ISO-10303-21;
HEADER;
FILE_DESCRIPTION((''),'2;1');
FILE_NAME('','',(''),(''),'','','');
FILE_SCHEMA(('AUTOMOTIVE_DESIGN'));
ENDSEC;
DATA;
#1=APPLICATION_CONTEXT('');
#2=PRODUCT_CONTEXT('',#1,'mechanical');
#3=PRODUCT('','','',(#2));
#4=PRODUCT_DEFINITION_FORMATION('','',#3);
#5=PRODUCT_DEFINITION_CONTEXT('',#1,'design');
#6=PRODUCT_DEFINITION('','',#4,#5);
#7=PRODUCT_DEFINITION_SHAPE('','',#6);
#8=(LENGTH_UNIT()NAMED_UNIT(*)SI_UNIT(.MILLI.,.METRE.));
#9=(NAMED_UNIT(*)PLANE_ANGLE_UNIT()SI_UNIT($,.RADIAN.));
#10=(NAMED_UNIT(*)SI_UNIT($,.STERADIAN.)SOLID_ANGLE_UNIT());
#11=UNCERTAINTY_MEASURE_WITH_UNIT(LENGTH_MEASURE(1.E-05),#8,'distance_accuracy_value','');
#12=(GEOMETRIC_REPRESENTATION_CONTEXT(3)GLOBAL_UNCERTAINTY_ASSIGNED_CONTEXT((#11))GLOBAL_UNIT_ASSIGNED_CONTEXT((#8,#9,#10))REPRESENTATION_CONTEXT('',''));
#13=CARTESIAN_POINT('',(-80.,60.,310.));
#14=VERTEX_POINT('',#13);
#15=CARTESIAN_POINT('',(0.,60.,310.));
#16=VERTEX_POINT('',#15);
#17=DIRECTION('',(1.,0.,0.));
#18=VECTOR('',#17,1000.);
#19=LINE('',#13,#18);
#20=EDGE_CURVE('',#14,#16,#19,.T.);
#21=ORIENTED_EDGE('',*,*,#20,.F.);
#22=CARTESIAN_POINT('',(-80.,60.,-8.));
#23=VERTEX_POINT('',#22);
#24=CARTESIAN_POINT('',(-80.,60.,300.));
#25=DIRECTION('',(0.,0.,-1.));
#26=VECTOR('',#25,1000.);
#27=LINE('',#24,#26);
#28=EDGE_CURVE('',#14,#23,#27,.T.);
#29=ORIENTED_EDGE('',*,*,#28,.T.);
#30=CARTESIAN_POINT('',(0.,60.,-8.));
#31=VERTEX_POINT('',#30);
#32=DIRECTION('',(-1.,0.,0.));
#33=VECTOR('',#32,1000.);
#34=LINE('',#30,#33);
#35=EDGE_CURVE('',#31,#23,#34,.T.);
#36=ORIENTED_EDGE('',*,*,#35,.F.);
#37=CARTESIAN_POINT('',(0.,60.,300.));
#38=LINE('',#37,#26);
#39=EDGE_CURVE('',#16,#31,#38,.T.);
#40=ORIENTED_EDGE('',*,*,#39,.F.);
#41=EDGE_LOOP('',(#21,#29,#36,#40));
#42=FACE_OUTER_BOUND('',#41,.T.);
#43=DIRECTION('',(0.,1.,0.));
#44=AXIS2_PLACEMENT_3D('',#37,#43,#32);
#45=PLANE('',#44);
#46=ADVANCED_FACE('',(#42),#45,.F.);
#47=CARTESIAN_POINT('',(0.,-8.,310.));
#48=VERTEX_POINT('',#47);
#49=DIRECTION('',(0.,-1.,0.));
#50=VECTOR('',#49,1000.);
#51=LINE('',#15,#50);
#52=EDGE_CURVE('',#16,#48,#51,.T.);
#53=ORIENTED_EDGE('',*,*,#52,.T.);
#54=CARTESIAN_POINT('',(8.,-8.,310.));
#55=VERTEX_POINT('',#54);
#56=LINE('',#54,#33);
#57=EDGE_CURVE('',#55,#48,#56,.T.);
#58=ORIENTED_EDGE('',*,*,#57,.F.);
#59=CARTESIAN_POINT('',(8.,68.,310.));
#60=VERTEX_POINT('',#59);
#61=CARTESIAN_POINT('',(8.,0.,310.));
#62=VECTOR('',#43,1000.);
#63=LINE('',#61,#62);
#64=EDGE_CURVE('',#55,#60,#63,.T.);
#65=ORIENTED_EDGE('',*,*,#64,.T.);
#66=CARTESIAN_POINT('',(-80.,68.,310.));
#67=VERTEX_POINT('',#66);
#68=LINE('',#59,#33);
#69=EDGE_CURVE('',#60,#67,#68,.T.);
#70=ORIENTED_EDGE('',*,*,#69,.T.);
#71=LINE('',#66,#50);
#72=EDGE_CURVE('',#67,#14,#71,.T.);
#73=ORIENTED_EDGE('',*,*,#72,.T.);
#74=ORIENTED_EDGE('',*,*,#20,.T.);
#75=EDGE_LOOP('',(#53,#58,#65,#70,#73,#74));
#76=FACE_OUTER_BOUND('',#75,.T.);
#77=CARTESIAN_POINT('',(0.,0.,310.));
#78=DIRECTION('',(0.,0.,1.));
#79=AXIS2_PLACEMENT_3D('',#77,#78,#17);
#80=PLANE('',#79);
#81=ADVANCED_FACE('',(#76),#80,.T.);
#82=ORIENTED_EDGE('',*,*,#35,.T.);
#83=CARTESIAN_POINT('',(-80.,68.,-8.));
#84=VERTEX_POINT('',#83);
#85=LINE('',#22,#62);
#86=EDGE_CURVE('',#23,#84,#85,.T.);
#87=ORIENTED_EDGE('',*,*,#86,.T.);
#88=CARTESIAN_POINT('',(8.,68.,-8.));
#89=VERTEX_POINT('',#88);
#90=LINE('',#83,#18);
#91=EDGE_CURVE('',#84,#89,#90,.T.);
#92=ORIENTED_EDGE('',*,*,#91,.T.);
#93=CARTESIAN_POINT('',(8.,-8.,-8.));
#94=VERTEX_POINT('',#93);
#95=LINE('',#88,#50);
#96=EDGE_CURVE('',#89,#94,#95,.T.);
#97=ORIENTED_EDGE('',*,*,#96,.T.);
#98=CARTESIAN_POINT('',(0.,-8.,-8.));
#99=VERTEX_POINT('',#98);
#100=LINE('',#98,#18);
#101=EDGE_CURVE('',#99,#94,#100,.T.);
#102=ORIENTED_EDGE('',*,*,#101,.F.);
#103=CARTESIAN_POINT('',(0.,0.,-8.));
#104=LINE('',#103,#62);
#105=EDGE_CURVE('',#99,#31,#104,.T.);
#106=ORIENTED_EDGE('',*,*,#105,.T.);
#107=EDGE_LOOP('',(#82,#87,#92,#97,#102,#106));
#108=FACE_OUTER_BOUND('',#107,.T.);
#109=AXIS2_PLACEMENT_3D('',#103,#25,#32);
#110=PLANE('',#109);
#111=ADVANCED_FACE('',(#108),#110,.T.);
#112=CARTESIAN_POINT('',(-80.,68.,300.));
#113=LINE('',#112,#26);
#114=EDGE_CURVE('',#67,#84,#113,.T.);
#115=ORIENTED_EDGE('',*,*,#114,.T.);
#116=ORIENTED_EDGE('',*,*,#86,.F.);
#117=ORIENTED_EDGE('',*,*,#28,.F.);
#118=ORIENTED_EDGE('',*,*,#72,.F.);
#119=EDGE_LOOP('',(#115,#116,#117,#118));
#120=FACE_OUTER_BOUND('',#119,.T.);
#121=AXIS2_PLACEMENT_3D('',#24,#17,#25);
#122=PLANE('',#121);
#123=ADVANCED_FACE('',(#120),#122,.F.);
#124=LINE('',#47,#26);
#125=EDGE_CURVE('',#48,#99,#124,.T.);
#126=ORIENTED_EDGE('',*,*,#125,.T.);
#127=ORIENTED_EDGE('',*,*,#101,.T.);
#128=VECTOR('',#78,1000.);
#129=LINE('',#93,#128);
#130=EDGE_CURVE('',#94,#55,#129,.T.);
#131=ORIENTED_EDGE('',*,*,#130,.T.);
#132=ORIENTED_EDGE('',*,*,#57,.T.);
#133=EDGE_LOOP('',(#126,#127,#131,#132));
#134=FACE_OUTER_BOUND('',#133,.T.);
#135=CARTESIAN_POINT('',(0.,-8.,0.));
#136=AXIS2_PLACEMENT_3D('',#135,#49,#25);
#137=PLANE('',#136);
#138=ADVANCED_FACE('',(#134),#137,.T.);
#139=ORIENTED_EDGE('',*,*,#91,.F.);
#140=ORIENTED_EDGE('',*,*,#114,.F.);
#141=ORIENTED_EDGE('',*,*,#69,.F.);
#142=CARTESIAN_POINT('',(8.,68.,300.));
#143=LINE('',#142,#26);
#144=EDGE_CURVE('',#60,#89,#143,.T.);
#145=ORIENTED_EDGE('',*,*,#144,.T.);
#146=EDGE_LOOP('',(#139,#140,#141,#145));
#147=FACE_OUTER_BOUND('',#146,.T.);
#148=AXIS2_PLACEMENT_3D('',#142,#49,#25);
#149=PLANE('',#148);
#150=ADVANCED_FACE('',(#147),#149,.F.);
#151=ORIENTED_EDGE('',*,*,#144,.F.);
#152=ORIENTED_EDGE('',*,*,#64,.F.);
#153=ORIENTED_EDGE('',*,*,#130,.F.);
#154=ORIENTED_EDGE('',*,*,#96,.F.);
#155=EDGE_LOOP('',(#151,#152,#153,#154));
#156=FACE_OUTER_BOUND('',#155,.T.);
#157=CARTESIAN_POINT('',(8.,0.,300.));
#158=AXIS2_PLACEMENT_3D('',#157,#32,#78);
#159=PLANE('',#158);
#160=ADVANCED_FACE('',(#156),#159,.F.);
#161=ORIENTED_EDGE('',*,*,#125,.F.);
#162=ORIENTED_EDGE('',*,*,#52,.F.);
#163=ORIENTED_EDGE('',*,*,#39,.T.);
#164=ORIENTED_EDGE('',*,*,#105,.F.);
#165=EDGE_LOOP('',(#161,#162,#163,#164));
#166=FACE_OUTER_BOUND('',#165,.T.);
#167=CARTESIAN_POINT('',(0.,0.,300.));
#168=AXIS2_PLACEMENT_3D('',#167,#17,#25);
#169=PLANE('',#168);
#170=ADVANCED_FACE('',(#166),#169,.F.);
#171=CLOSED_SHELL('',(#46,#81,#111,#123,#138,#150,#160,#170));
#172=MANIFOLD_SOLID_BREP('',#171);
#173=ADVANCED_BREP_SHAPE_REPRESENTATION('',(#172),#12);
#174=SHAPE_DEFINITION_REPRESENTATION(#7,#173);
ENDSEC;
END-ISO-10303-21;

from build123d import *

# Parameters (mm, degrees)
EXTRUDE_1_DEPTH = 300
EXTRUDE_2_DEPTH = 10
EXTRUDE_3_DEPTH = 8
SKETCH_5_W      = 8
SKETCH_5_H      = 318
EXTRUDE_4_DEPTH = 8


with BuildPart() as part:
    # 草图1 → 凸台-拉伸1 (new body)
    with BuildSketch(Plane.XY):
        Polygon((0, 0), (0, 60), (-80, 60), (-80, 68), (8, 68), (8, 0), align=None)
    extrude(amount=EXTRUDE_1_DEPTH)

    # 草图2 → 凸台-拉伸2 (add)
    with BuildSketch(Plane.XY.offset(300)):
        Polygon((0, 0), (8, 0), (8, 68), (-80, 68), (-80, 60), (0, 60), align=None)
    extrude(amount=EXTRUDE_2_DEPTH)

    # 草图4 → 凸台-拉伸3 (add)
    with BuildSketch(Plane(origin=(0, 0, 0), x_dir=(-1, 0, 0), z_dir=(0, 0, -1))):
        Polygon((-8, 0), (0, 0), (0, 60), (80, 60), (80, 68), (-8, 68), align=None)
    extrude(amount=EXTRUDE_3_DEPTH)

    # 草图5 → 凸台-拉伸4 (add)
    with BuildSketch(Plane.XZ):
        with Locations((4, 151)):
            Rectangle(SKETCH_5_W, SKETCH_5_H)
    extrude(amount=EXTRUDE_4_DEPTH)


solid = part.part
